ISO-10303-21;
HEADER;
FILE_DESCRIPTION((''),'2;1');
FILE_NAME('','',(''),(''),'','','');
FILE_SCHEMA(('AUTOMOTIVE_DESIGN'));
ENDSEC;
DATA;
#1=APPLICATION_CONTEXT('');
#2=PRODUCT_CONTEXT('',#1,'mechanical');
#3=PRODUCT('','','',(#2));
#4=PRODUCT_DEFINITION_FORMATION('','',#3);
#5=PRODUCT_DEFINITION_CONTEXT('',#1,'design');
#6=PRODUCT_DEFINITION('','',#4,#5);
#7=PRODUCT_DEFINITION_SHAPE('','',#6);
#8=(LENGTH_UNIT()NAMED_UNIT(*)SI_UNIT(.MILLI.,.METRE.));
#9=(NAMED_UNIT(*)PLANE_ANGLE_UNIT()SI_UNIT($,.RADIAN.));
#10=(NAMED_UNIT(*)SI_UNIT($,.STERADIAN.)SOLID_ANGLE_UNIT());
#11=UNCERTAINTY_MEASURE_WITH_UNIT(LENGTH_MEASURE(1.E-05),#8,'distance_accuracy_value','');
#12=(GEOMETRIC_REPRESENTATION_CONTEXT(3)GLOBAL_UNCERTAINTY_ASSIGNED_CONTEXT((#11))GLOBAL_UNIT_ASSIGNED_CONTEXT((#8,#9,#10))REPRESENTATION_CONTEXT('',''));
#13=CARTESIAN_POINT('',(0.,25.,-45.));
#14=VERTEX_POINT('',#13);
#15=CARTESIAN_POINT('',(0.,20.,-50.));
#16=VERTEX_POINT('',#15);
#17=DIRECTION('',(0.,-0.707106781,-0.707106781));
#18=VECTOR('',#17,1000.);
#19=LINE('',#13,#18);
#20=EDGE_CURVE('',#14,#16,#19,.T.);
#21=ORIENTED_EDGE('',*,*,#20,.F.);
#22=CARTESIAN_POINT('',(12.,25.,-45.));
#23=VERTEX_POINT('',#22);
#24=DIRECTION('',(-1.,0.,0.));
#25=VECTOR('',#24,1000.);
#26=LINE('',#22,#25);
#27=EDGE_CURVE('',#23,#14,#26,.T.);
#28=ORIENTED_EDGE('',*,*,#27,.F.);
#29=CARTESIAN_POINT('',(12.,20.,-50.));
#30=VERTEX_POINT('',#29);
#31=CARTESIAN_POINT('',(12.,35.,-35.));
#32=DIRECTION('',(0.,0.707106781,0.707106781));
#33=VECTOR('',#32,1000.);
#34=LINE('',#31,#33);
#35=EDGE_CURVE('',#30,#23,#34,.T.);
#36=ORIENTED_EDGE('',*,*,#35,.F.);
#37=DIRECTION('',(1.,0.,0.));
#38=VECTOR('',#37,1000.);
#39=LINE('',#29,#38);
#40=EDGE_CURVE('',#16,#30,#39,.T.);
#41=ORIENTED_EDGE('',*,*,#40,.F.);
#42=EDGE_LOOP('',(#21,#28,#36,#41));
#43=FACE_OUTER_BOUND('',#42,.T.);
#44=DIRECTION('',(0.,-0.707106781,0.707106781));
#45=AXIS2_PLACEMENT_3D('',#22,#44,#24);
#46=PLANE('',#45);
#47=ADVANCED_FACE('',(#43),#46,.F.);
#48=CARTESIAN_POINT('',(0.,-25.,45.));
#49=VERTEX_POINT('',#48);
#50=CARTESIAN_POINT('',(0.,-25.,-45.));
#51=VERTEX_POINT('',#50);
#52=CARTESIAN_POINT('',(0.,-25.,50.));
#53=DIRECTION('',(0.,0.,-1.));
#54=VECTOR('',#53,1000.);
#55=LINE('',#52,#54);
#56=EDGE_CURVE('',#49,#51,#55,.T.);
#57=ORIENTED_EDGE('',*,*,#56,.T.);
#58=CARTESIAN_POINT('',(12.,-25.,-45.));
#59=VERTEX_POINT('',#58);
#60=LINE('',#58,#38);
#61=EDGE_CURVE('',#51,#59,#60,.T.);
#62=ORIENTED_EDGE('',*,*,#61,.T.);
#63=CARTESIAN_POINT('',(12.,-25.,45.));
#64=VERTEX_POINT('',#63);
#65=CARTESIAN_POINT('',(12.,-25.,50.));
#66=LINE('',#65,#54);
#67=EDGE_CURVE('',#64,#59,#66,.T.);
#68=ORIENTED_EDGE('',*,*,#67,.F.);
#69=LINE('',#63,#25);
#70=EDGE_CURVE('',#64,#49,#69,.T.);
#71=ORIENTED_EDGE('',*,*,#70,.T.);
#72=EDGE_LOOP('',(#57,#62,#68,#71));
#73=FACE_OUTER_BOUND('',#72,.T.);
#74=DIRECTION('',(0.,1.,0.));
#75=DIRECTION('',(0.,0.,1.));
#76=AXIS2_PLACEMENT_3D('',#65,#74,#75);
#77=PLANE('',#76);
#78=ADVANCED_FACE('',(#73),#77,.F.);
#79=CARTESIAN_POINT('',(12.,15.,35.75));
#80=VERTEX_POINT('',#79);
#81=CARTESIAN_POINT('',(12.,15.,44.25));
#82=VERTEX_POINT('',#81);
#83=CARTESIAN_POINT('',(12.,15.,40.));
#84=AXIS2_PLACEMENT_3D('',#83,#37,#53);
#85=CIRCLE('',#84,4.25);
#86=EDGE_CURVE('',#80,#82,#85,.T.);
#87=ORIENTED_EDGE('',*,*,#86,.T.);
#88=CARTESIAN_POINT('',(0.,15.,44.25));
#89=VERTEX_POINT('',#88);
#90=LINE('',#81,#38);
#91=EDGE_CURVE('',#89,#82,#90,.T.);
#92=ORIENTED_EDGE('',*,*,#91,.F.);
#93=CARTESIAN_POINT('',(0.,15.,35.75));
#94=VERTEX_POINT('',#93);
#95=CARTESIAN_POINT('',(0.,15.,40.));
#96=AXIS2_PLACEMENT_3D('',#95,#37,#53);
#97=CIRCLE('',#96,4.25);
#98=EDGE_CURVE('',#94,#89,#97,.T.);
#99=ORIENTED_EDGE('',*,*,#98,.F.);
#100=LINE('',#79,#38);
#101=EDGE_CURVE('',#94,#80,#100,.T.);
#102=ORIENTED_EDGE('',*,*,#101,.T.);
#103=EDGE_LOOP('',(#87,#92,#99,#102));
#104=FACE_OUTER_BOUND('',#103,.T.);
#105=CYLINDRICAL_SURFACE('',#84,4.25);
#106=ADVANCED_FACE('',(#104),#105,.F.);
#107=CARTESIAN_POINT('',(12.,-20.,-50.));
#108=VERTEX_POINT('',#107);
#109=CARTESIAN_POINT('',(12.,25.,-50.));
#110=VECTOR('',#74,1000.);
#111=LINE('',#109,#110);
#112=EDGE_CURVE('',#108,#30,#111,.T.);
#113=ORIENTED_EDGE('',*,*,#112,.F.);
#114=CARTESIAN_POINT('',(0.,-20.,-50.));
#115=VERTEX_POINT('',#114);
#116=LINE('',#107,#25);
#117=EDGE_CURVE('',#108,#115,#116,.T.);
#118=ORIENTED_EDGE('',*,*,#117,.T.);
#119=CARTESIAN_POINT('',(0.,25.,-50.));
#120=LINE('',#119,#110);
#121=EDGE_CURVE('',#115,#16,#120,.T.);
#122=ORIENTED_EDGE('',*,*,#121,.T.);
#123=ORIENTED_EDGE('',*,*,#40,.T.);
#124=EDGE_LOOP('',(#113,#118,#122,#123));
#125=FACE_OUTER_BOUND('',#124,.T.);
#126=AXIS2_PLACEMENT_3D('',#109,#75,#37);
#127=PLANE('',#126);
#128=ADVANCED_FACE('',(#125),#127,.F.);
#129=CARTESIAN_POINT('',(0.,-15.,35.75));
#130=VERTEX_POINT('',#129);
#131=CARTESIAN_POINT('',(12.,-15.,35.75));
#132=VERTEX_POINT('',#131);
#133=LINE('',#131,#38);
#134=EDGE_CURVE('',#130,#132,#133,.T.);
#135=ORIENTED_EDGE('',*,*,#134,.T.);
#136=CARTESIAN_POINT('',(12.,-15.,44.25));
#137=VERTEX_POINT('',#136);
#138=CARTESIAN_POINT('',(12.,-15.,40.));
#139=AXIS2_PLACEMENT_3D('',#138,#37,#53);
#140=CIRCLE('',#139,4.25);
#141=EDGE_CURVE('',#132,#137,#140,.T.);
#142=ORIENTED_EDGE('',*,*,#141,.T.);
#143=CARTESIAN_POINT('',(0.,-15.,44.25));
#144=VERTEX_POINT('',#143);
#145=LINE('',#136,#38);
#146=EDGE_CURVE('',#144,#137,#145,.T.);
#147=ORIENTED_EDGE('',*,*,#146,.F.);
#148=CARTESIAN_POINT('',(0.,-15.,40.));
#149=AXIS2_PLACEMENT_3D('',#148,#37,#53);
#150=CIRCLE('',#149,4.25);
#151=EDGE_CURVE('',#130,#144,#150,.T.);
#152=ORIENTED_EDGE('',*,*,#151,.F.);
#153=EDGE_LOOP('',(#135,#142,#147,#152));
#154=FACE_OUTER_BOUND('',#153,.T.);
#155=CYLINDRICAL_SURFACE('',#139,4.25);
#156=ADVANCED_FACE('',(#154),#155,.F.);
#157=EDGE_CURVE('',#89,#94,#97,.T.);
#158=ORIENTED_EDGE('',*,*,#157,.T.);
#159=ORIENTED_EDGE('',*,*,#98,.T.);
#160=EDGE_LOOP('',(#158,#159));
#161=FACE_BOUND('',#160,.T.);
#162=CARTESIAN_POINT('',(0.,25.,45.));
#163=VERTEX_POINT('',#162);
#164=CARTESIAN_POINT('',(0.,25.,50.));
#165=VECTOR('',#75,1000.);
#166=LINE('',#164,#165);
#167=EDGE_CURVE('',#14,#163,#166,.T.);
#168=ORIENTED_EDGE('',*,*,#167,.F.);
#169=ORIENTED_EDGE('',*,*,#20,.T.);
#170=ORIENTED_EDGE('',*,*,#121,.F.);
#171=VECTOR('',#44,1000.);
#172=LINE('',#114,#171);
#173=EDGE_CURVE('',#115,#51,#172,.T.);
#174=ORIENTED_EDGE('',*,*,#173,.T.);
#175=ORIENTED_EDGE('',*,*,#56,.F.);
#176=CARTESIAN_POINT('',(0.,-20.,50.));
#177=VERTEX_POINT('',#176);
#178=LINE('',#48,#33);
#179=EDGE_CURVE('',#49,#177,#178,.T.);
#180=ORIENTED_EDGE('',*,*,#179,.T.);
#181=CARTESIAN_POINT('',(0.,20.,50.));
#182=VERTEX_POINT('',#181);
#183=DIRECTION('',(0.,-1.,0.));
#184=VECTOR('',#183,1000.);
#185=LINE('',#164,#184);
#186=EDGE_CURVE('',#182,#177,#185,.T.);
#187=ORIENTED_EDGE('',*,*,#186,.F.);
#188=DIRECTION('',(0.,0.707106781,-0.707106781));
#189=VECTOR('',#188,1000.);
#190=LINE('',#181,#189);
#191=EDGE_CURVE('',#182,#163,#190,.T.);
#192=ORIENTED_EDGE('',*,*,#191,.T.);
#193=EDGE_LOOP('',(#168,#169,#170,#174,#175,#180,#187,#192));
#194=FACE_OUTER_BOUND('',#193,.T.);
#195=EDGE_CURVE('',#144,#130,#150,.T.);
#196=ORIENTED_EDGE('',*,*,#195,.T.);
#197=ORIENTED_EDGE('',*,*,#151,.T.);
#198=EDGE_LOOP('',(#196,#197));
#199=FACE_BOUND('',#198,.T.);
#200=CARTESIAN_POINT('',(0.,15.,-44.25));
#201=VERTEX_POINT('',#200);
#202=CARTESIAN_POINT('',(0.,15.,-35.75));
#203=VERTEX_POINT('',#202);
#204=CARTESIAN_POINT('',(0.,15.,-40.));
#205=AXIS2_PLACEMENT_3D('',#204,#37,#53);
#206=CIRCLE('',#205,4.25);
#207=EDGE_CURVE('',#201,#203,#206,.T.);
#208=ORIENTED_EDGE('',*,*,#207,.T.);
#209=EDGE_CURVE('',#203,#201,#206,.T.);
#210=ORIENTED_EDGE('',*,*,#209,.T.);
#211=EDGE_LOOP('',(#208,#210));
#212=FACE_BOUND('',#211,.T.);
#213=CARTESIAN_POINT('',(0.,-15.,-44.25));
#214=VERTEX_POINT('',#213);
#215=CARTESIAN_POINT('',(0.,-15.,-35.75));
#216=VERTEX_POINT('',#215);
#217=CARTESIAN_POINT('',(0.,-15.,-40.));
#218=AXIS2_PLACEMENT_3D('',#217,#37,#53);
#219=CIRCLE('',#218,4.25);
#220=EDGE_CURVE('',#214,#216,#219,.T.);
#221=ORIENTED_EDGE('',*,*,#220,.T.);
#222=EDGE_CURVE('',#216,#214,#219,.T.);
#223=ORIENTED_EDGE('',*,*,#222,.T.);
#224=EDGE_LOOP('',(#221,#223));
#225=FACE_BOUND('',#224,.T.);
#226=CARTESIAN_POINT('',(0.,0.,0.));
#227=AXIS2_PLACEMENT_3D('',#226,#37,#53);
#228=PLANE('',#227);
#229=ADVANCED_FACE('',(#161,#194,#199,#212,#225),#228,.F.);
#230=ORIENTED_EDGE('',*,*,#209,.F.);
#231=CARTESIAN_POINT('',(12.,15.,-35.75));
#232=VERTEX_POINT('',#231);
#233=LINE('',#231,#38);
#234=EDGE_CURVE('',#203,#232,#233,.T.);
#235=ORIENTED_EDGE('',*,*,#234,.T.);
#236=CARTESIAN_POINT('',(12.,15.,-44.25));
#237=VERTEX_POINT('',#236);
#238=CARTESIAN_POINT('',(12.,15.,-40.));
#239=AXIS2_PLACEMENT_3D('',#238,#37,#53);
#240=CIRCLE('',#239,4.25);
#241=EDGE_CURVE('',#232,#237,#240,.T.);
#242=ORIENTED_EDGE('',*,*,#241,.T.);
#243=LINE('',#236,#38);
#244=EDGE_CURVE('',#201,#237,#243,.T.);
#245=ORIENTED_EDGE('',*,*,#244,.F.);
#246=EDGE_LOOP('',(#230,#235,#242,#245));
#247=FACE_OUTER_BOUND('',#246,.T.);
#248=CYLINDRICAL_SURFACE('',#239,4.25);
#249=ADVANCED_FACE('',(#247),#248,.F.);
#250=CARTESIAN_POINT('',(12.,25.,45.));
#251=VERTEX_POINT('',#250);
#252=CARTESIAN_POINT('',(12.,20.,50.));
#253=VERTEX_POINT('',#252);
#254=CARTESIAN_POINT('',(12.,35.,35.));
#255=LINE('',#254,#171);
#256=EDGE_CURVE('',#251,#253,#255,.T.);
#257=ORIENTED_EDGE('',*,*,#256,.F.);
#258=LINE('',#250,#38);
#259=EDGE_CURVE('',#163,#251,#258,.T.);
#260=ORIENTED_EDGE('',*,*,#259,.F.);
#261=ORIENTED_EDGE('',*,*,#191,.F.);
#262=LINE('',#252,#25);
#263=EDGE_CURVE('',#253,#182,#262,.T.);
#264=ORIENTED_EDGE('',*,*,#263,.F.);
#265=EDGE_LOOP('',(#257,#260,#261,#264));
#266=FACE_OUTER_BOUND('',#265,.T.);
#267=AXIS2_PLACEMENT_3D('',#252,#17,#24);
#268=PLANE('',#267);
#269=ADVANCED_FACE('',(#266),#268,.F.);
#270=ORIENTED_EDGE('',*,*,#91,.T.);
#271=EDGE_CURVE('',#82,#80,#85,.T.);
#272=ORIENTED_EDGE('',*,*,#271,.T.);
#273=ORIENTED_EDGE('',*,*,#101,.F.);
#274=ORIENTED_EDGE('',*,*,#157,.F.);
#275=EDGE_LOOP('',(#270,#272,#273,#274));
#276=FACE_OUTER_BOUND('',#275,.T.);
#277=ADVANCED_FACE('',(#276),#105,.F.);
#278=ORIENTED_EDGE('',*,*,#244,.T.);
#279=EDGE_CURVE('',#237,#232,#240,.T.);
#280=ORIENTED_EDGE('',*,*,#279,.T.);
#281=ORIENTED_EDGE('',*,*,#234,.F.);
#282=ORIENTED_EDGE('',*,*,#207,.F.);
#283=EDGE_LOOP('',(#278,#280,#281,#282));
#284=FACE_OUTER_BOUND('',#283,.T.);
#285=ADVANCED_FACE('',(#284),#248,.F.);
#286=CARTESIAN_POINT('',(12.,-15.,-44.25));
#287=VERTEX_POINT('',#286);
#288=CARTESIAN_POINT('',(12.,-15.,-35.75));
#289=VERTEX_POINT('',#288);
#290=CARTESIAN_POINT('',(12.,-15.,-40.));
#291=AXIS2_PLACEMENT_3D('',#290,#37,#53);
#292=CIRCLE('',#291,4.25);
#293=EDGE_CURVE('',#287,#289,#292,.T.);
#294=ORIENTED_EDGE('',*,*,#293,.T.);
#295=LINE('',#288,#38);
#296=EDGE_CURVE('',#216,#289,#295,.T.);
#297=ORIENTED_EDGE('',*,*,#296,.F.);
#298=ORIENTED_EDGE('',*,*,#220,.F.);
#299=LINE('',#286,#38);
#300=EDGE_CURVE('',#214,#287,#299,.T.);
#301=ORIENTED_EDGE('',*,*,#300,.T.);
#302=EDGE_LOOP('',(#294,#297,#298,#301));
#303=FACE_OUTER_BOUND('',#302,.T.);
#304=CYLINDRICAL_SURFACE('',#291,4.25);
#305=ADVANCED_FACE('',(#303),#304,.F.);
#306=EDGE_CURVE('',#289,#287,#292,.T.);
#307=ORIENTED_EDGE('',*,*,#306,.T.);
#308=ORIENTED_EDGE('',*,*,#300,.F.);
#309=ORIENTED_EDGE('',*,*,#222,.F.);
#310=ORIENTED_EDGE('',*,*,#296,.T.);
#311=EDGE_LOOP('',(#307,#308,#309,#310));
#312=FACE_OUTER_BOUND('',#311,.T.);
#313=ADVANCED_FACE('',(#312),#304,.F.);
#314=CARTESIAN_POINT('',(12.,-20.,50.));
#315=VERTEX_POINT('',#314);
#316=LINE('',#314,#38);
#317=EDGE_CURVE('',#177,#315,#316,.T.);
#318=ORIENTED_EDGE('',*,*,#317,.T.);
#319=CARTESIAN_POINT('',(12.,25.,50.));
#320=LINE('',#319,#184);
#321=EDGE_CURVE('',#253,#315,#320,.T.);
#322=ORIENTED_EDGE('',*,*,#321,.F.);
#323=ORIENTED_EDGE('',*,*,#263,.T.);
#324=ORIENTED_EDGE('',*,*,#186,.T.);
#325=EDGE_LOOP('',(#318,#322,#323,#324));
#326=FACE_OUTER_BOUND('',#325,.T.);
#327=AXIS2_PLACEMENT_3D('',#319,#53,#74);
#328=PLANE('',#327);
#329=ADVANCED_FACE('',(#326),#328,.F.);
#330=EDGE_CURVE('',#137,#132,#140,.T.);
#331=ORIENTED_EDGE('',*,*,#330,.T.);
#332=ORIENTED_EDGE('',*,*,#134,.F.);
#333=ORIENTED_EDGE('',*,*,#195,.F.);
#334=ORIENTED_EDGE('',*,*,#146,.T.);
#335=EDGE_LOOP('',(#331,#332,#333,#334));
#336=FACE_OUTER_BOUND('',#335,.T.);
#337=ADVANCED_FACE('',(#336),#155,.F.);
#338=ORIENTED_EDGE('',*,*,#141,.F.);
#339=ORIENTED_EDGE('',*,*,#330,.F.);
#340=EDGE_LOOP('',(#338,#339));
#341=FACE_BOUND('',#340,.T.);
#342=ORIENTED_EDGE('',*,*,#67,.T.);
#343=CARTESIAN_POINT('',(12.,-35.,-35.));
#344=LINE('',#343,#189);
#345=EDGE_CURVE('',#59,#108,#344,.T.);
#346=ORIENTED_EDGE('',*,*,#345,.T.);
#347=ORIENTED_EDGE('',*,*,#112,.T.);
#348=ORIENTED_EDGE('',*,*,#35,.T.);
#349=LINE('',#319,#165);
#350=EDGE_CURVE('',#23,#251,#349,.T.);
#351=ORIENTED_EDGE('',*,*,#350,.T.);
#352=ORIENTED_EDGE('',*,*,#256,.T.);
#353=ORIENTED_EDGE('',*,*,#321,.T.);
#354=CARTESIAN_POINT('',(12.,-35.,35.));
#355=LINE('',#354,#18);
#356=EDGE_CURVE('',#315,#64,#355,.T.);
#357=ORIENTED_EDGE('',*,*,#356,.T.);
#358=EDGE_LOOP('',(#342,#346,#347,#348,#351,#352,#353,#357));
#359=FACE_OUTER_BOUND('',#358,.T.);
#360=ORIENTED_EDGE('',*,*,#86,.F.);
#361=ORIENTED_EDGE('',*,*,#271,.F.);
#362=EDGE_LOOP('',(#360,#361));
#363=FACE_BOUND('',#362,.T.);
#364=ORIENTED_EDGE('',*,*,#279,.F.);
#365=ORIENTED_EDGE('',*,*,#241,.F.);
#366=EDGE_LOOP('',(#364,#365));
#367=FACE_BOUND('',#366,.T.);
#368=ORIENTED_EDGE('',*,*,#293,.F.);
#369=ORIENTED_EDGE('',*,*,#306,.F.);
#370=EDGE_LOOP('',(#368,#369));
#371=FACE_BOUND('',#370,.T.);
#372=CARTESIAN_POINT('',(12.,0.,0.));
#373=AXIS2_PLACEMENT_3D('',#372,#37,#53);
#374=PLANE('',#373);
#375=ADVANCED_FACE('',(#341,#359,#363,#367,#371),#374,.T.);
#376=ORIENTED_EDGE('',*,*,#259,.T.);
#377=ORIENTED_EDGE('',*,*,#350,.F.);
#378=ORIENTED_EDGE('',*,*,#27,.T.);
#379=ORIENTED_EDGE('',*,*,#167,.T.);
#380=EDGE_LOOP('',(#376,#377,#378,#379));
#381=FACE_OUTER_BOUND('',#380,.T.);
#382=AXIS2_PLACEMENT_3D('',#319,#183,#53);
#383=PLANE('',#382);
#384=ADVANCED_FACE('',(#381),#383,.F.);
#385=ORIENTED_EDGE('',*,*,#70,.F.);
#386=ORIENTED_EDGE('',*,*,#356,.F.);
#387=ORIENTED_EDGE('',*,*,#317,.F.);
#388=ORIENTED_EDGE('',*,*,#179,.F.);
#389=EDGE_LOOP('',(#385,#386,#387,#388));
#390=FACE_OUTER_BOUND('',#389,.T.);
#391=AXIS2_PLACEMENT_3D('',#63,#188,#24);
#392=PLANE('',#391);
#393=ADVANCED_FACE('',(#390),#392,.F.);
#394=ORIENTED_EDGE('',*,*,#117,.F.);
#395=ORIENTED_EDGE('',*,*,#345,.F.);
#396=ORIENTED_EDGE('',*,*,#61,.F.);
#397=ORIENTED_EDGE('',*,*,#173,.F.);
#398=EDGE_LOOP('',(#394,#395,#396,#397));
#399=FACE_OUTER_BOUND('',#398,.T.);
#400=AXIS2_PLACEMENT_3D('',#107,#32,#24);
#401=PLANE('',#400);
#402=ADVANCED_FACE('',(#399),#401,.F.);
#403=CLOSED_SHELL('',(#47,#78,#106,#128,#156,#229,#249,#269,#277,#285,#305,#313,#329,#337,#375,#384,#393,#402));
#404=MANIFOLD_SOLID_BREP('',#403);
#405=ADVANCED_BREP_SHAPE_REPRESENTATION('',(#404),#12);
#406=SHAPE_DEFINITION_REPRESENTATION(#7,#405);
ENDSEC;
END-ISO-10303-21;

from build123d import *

# Parameters (mm, degrees)
SKETCH_1_W              = 100
SKETCH_1_H              = 50
EXTRUDE_1_DEPTH         = 12
HOLE_WIZARD_8_5_8_5_1_D = 8.5
CHAMFER_1_SIZE          = 5


with BuildPart() as part:
    # 草图1 → 凸台-拉伸1 (new body)
    with BuildSketch(Plane(origin=(0, 0, 0), x_dir=(0, 0, -1), z_dir=(1, 0, 0))):
        Rectangle(SKETCH_1_W, SKETCH_1_H)
    extrude(amount=EXTRUDE_1_DEPTH)

    # Ø8.5 (8.5) 直径孔1 (through all)
    with Locations(Plane(origin=(12, 0, 0), x_dir=(0, 0, -1), z_dir=(1, 0, 0))):
        with Locations((-40, 15), (-40, -15), (40, 15), (40, -15)):
            Hole(HOLE_WIZARD_8_5_8_5_1_D / 2)

    # 倒角1
    chamfer_1_edges = [part.edges().sort_by_distance(p)[0] for p in [
        (6, -25, -50),
        (6, -25, 50),
        (6, 25, 50),
        (6, 25, -50),
    ]]
    chamfer(chamfer_1_edges, length=CHAMFER_1_SIZE)


solid = part.part
